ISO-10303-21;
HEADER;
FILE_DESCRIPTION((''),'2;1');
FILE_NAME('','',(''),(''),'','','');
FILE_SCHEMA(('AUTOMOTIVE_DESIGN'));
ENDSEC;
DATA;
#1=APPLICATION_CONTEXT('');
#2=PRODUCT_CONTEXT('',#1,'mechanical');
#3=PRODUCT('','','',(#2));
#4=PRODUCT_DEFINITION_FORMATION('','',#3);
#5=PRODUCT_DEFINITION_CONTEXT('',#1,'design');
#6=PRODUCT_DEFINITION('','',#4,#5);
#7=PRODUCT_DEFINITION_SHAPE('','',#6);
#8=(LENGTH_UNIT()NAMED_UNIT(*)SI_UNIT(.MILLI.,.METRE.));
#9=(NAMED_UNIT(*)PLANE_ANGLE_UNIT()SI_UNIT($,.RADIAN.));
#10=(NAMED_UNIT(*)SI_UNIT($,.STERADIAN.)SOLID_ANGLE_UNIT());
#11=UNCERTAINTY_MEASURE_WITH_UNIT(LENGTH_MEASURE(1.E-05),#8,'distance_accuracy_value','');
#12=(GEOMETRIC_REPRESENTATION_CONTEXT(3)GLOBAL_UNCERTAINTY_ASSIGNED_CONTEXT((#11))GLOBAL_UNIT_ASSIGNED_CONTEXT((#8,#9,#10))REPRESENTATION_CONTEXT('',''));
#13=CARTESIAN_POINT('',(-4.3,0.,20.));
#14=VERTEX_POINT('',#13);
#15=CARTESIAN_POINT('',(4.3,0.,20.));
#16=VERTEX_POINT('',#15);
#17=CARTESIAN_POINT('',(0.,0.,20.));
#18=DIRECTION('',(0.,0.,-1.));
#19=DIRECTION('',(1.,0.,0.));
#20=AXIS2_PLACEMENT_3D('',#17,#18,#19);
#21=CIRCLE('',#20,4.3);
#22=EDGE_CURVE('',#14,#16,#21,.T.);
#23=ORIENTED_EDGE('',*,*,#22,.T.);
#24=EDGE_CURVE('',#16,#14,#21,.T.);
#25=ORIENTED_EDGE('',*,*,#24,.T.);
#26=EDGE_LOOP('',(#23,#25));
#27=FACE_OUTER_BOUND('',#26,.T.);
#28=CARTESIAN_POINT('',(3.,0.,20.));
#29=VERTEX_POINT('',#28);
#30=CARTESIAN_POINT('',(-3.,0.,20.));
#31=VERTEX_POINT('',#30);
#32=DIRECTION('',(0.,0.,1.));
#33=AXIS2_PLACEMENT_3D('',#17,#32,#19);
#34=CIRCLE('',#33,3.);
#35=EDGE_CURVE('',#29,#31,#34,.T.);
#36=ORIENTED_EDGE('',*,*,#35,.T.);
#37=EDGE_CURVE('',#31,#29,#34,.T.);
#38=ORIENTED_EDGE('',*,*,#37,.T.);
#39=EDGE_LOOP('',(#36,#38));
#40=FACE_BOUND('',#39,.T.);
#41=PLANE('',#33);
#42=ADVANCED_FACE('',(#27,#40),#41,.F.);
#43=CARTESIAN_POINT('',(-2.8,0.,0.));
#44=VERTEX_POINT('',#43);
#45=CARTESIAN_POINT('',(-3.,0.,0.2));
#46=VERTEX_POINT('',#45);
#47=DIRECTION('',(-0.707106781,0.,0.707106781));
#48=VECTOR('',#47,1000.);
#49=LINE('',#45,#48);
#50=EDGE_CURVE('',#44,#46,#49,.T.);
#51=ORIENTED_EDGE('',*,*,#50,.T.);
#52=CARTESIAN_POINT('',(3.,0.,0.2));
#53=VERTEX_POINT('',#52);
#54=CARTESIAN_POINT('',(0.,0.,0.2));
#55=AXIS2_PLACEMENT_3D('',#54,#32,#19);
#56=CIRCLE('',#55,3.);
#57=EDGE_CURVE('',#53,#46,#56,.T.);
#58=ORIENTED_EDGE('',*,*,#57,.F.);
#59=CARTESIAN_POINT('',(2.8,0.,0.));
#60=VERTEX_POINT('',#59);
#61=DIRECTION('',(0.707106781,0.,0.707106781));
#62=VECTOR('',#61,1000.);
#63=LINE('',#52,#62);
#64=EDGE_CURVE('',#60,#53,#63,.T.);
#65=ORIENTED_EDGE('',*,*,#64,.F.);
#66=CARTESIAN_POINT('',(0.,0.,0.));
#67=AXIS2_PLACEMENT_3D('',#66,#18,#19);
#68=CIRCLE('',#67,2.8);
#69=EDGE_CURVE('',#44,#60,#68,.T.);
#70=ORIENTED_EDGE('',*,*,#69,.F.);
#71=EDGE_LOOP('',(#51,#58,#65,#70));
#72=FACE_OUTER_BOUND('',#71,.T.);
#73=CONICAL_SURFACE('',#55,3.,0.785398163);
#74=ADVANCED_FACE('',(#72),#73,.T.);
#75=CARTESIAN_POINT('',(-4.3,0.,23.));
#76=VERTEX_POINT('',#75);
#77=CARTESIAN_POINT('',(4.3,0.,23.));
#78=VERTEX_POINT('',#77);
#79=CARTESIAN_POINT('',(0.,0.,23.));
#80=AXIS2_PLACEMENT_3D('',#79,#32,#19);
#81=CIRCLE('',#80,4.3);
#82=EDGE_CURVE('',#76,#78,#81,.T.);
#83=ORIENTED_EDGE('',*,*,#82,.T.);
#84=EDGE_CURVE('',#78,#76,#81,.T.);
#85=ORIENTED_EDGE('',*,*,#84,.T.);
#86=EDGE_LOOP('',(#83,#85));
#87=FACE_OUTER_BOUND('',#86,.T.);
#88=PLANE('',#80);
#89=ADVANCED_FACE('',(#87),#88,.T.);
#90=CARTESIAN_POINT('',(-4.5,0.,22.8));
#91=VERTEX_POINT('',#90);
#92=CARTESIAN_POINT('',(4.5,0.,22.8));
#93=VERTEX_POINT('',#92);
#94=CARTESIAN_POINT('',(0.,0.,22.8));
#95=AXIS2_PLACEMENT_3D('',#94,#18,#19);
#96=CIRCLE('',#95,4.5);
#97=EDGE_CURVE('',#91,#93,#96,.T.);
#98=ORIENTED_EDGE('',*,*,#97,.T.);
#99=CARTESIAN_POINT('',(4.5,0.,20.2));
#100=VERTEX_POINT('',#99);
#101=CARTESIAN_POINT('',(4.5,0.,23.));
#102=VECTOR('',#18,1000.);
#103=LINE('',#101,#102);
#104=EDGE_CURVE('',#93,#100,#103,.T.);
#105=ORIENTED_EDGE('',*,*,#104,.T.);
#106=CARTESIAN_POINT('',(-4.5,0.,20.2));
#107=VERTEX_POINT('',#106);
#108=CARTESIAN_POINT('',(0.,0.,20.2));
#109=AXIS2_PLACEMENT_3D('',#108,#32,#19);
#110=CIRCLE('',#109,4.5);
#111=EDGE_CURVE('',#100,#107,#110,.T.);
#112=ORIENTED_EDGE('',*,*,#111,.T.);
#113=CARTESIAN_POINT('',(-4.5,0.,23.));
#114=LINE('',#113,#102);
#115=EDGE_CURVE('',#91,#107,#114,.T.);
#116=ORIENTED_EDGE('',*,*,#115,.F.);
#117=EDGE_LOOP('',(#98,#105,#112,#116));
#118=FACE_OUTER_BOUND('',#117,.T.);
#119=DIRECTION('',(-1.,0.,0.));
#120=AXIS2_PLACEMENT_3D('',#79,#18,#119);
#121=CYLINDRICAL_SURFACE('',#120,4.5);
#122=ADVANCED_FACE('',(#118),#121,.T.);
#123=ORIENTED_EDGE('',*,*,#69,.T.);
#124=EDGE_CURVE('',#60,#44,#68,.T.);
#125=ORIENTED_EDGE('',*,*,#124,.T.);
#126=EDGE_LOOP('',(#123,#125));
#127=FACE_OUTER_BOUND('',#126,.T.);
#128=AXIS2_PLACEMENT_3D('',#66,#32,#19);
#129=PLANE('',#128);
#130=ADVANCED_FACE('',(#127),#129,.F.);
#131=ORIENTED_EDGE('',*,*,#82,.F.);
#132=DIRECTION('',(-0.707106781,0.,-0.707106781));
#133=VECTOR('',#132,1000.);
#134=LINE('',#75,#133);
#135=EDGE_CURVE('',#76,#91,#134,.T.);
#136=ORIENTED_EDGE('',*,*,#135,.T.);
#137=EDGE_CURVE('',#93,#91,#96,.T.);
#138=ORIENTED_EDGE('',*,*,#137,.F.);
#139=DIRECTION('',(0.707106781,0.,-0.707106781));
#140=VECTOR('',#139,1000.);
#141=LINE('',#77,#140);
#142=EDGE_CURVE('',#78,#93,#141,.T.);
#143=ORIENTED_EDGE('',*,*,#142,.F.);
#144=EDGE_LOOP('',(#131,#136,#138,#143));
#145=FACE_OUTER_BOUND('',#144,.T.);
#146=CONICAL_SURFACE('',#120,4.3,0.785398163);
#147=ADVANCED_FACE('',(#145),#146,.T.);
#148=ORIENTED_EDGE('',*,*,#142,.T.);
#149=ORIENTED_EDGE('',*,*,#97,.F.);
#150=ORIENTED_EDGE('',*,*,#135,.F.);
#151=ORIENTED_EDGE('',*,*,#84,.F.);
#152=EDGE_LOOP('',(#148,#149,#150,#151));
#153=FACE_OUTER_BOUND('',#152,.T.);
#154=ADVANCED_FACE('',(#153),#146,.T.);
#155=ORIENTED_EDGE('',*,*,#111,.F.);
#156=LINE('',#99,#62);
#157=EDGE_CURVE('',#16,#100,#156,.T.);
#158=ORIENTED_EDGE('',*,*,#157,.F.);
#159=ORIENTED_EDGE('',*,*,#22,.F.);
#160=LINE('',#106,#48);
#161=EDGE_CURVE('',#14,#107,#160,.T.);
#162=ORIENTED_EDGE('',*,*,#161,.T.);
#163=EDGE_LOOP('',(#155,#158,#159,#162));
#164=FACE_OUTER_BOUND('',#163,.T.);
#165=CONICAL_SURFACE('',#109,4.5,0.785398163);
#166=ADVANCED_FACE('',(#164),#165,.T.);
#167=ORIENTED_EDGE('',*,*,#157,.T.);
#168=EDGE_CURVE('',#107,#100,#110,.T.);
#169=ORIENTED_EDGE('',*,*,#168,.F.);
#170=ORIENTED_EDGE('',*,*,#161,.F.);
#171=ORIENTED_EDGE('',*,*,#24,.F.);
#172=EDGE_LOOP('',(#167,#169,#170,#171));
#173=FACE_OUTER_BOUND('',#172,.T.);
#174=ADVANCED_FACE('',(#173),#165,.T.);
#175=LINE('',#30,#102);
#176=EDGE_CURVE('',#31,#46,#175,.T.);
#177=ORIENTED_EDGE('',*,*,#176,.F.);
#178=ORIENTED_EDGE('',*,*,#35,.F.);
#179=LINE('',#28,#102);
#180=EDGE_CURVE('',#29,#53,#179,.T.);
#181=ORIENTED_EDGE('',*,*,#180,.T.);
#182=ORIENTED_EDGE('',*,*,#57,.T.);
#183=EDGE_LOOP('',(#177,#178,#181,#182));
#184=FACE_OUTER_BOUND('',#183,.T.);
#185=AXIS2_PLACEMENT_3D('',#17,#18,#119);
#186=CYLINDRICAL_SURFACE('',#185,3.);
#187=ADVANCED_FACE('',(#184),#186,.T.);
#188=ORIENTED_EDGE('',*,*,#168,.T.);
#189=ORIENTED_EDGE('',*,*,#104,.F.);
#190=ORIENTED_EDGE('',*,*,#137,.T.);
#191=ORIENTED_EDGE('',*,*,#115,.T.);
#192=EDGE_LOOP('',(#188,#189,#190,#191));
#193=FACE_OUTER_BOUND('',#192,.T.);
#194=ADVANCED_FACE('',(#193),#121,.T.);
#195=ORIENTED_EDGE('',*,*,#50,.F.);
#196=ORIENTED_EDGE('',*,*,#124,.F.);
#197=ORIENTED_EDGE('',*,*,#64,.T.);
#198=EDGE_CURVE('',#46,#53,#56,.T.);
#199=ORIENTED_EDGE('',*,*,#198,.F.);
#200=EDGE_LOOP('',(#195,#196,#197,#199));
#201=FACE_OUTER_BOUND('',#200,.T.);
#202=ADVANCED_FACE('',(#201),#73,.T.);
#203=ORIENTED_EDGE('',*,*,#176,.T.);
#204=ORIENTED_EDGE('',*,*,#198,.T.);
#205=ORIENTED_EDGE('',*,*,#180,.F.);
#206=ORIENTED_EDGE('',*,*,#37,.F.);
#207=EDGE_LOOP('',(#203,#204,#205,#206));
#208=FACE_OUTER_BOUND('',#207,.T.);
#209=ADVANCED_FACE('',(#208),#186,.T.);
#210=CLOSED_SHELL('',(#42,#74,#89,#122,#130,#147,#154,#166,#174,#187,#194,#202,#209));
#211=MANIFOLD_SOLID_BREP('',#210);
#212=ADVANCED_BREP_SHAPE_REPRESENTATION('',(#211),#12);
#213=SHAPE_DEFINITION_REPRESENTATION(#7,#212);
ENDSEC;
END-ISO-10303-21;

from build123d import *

# Parameters (mm, degrees)
SKETCH1_R           = 3
BOSS_EXTRUDE1_DEPTH = 20
SKETCH2_R           = 4.5
BOSS_EXTRUDE2_DEPTH = 3
CHAMFER1_SIZE       = 0.2


with BuildPart() as part:
    # Sketch1 → Boss-Extrude1 (new body)
    with BuildSketch(Plane.XY):
        Circle(SKETCH1_R)
    extrude(amount=BOSS_EXTRUDE1_DEPTH)

    # Sketch2 → Boss-Extrude2 (add)
    with BuildSketch(Plane.XY.offset(20)):
        Circle(SKETCH2_R)
    extrude(amount=BOSS_EXTRUDE2_DEPTH)

    # Chamfer1
    chamfer1_edges = [part.edges().sort_by_distance(p)[0] for p in [
        (-3, 0, 0),
        (-4.5, 0, 20),
        (-4.5, 0, 23),
    ]]
    chamfer(chamfer1_edges, length=CHAMFER1_SIZE)


solid = part.part
